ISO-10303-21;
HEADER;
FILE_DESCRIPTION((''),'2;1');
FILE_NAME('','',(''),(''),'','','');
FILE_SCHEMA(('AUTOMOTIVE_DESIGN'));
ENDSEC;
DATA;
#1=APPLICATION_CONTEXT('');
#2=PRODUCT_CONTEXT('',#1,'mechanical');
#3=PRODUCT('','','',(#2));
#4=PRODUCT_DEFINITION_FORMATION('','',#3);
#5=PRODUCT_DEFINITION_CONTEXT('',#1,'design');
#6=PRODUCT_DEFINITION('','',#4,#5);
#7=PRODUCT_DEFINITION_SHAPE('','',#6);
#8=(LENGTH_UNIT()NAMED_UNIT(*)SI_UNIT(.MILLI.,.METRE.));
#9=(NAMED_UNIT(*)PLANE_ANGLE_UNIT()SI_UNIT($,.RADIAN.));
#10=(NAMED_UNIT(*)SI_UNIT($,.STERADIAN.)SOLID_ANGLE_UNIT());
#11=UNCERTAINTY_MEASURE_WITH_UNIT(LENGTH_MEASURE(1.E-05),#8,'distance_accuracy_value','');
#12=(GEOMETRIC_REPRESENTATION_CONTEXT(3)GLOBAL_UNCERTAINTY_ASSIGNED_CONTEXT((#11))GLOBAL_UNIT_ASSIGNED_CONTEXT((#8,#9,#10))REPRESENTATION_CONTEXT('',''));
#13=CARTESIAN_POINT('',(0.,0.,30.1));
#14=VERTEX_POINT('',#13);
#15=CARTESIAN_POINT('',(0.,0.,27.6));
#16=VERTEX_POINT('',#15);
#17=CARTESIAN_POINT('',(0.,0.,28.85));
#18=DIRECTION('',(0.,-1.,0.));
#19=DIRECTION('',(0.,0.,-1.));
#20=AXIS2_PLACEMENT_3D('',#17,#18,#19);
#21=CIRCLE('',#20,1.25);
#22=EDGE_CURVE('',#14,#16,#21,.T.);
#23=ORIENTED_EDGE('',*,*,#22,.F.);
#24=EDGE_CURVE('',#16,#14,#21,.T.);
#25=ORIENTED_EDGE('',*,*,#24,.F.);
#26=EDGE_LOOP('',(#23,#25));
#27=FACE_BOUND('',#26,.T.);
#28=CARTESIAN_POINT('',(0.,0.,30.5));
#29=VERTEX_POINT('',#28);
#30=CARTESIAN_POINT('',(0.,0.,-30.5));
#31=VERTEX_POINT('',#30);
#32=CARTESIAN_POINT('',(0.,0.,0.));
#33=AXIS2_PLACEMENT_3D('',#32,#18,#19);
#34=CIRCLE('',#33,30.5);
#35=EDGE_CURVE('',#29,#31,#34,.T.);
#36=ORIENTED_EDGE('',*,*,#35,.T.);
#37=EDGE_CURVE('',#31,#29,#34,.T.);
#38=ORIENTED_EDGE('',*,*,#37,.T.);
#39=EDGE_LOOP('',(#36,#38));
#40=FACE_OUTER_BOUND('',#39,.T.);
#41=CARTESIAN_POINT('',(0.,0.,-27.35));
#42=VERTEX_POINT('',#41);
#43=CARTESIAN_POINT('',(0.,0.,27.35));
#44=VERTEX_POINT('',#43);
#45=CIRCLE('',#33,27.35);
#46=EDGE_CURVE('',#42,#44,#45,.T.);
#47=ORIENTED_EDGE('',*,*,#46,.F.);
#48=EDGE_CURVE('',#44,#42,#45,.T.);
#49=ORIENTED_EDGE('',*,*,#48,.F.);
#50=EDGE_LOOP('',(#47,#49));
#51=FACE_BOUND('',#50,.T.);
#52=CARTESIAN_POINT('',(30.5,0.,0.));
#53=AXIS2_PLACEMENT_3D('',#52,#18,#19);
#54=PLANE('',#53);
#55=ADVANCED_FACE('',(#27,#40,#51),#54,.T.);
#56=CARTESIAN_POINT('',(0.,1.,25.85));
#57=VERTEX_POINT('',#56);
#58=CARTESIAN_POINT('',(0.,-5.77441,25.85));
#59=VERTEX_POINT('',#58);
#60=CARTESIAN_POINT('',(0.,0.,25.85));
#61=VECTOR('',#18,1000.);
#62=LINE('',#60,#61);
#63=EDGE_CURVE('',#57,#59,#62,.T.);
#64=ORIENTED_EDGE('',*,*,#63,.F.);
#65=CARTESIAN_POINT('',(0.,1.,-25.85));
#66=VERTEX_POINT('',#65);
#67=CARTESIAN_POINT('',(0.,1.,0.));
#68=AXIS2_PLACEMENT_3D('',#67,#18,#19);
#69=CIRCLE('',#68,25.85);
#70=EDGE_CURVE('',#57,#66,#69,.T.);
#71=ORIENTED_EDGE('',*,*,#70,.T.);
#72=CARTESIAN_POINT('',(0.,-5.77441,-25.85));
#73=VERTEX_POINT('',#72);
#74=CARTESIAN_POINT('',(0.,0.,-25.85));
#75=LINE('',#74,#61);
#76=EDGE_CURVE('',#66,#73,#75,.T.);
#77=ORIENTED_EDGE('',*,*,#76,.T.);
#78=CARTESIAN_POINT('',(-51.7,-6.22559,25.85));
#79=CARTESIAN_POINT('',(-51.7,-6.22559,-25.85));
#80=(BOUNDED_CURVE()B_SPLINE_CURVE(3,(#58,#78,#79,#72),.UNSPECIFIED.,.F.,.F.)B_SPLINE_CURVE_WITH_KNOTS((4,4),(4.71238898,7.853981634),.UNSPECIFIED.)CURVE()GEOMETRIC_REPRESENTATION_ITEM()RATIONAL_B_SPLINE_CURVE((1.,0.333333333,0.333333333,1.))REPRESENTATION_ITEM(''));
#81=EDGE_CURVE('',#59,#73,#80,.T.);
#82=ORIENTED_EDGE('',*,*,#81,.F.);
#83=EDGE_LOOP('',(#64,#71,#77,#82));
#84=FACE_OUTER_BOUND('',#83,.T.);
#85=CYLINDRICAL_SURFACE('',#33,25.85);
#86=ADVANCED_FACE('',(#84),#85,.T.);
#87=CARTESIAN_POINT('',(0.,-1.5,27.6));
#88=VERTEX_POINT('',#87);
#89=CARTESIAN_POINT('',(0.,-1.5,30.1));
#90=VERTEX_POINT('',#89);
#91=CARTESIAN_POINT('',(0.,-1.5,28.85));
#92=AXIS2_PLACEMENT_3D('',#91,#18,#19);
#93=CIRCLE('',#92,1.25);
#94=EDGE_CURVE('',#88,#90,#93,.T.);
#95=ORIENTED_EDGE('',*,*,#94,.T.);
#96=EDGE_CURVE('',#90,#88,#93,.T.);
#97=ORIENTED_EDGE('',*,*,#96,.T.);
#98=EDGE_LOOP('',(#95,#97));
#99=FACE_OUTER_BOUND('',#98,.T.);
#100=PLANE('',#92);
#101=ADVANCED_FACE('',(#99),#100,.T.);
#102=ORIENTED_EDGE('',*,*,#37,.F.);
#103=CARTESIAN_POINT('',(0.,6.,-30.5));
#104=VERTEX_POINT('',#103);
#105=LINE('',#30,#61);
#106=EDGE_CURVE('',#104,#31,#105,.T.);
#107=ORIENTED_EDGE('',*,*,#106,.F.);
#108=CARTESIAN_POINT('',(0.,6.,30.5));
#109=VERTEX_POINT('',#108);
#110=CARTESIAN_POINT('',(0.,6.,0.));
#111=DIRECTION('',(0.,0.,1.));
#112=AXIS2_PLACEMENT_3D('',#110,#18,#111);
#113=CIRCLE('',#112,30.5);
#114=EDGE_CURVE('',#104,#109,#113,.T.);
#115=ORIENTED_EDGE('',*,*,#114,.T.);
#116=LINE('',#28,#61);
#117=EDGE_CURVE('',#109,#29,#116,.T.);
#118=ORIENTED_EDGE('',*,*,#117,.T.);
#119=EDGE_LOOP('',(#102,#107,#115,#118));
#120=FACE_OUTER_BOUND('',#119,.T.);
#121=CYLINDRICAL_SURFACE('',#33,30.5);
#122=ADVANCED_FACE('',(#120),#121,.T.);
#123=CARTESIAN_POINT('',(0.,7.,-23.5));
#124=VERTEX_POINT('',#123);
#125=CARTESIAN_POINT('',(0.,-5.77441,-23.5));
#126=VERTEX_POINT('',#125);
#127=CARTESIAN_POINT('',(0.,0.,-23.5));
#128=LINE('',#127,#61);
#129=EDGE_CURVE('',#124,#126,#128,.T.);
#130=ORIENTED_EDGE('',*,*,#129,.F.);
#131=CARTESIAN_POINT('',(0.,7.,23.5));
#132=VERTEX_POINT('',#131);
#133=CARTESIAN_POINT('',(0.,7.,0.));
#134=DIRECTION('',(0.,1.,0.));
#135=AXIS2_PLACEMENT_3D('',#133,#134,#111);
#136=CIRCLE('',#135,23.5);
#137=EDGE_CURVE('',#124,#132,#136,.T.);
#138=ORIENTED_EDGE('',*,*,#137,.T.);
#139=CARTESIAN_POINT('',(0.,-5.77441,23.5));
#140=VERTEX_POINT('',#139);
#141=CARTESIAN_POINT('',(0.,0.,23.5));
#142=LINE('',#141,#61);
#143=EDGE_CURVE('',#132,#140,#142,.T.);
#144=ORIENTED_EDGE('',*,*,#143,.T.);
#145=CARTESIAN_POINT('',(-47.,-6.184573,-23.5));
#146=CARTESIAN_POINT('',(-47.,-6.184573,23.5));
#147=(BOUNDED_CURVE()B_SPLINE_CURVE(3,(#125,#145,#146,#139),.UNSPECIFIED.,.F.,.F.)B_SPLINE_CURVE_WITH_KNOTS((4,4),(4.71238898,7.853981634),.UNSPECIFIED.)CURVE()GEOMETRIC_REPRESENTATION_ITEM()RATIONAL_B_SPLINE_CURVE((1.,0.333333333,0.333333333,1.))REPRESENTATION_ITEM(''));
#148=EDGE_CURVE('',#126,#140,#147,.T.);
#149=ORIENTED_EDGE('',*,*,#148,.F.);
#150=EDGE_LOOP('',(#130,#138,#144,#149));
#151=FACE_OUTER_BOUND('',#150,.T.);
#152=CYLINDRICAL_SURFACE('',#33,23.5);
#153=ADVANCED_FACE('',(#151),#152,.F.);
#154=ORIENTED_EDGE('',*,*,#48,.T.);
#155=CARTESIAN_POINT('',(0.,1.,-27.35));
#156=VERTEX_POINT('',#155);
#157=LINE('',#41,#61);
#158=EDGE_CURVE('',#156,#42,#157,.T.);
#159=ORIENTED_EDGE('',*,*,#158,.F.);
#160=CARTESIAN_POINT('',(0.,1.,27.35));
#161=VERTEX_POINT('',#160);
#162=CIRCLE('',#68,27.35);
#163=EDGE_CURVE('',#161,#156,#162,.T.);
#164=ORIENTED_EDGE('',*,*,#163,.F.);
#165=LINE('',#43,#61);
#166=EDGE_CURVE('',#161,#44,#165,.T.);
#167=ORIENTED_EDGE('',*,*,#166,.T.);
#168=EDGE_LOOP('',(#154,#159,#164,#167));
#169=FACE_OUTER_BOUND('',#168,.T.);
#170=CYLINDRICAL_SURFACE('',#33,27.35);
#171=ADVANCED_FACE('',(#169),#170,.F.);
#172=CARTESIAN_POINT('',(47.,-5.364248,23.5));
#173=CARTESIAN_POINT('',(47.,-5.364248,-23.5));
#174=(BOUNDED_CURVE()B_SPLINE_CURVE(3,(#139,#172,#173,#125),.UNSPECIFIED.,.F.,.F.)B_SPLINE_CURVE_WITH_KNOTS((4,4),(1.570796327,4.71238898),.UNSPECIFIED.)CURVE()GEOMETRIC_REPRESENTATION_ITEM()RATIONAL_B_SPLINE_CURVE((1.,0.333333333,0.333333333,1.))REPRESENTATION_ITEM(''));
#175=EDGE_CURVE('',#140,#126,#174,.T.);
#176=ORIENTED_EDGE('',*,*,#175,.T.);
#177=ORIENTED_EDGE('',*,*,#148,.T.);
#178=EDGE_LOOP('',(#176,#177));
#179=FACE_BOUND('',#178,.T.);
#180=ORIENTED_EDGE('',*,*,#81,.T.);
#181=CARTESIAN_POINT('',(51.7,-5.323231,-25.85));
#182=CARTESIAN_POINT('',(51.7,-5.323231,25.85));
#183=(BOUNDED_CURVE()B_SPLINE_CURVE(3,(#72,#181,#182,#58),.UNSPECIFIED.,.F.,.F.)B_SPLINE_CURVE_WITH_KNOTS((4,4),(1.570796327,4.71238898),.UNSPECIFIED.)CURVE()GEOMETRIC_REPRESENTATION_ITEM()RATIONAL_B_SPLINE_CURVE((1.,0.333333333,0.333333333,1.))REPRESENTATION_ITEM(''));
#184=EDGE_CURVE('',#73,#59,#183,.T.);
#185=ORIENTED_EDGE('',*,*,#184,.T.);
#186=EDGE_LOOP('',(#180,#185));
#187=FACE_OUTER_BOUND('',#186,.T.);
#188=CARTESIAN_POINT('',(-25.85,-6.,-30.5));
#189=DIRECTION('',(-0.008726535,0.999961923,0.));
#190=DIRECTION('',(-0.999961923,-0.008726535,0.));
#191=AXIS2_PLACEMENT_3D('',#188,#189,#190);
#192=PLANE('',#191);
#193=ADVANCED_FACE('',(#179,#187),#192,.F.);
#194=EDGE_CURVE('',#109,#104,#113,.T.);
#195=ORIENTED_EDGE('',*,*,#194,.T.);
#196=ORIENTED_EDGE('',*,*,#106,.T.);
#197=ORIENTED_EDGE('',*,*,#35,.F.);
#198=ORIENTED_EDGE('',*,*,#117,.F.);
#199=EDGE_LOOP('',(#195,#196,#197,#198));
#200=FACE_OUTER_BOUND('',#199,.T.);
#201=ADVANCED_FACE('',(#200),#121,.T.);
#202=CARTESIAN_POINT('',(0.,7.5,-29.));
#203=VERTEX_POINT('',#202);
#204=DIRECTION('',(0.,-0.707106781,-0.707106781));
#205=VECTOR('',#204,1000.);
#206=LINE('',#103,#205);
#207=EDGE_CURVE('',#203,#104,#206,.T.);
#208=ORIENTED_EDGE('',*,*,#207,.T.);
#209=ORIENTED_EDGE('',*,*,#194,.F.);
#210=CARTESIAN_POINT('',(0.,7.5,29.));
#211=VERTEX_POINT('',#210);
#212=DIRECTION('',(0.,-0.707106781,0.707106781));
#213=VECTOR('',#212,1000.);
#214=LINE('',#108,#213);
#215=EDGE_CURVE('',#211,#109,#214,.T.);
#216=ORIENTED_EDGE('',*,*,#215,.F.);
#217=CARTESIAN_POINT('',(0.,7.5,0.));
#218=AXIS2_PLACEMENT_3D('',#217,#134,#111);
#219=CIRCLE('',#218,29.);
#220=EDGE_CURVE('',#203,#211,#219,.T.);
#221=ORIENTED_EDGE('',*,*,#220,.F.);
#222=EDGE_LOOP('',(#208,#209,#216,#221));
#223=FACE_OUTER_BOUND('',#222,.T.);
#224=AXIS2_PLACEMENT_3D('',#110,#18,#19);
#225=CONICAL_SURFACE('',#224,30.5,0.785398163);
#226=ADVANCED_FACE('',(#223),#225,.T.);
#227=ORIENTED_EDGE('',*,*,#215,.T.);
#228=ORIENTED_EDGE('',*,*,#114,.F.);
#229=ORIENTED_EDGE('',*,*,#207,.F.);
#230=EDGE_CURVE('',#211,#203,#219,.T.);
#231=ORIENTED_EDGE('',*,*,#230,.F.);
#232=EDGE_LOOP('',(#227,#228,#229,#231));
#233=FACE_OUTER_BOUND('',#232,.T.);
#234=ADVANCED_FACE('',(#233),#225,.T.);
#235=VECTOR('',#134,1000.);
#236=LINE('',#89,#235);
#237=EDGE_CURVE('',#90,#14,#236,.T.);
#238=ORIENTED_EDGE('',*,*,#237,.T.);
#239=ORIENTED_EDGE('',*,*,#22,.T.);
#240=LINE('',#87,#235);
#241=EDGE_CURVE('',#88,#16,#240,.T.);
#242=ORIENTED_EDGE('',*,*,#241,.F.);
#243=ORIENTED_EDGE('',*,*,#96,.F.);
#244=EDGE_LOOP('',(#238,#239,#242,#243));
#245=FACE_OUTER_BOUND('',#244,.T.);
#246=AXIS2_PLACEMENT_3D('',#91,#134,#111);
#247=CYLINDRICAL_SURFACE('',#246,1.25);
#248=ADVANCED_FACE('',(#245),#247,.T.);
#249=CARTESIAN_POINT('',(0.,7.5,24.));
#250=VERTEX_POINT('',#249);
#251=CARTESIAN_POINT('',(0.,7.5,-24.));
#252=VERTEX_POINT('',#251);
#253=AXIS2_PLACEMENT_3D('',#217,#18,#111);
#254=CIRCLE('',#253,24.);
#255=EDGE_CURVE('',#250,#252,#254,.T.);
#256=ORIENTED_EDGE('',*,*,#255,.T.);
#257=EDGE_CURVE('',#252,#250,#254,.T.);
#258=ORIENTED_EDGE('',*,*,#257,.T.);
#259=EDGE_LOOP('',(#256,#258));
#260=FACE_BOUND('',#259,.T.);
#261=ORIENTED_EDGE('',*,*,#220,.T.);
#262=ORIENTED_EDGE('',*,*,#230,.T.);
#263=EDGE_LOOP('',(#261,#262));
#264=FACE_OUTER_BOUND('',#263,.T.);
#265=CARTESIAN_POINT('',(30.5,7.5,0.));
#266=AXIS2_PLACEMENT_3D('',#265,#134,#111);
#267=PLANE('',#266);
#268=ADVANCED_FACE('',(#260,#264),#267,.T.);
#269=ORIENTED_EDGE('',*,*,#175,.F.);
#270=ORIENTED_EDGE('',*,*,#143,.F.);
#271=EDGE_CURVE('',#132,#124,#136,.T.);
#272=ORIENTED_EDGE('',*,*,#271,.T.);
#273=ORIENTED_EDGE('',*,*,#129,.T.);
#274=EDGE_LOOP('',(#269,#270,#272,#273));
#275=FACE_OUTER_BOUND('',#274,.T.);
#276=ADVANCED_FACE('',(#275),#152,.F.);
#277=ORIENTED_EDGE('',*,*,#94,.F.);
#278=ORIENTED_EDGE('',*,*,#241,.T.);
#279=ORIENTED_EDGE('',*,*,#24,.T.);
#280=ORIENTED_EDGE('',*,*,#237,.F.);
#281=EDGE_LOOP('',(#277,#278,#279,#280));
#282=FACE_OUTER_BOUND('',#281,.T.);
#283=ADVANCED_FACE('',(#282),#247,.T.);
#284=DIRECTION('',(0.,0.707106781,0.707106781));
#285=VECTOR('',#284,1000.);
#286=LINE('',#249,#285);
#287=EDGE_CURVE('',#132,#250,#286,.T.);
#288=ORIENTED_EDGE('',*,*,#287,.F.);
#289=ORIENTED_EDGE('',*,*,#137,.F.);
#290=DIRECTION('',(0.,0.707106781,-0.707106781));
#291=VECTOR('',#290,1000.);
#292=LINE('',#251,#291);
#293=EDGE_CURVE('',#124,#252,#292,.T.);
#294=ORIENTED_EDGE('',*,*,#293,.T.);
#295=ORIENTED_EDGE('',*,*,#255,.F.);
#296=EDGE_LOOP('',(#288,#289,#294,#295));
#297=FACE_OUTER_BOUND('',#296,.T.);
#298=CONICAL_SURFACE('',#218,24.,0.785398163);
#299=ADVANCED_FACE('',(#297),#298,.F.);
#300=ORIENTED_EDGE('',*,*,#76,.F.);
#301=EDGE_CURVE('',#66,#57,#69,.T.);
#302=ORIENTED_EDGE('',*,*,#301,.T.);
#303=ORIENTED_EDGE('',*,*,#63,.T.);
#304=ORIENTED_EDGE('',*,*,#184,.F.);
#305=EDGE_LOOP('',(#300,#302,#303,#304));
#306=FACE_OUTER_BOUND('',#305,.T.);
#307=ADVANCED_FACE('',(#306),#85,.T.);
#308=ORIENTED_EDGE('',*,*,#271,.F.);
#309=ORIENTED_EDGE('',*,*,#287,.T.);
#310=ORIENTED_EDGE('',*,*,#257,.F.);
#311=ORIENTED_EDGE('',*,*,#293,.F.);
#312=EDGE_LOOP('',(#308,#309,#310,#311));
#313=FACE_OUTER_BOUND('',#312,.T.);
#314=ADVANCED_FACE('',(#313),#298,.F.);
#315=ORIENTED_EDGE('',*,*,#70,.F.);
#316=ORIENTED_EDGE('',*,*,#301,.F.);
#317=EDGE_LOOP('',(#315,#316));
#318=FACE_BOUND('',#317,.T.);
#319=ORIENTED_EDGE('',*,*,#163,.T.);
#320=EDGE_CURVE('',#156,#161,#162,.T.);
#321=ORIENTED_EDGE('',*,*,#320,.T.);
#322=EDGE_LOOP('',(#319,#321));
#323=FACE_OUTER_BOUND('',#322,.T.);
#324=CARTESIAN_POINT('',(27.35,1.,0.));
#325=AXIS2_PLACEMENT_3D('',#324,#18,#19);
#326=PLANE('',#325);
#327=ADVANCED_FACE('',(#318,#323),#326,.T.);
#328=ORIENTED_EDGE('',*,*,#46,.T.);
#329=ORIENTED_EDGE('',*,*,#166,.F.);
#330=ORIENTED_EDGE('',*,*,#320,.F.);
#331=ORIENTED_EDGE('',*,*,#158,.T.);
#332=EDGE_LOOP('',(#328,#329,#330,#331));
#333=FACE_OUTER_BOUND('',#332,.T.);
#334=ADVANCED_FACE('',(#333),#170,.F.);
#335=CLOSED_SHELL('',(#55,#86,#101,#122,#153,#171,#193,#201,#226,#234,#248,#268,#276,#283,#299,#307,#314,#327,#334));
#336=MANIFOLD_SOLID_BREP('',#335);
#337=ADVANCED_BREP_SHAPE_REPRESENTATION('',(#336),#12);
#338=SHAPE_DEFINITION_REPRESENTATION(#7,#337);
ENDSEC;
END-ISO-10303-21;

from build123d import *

# Parameters (mm, degrees)
CUT_EXTRUDE_1_DEPTH      = 44.780703512
CUT_EXTRUDE_1_DEPTH_BACK = 44.780703512
CHAMFER_1_SIZE           = 0.5
CHAMFER_2_SIZE           = 1.5
SKETCH_3_R               = 1.25
EXTRUDE_1_DEPTH          = 1.5


with BuildPart() as part:
    # 草图1 → 旋转1 (revolve)
    with BuildSketch(Plane.XY, mode=Mode.PRIVATE) as revolve_1_sk:
        Polygon((23.5, -7.5), (23.5, 7.5), (30.5, 7.5), (30.5, 0), (27.35, 0), (27.35, 1), (25.85, 1), (25.85, -7.5), align=None)
    revolve(revolve_1_sk.sketch.rotate(Axis((0, 0, 0), (0, 1, 0)), 90), axis=Axis((0, 0, 0), (0, 1, 0)))

    # 草图2 → 切除-拉伸1 (cut, two sides: drawn at the far end of the back side and taken through both)
    with BuildSketch(Plane.XY.offset(-CUT_EXTRUDE_1_DEPTH_BACK)):
        Polygon((-25.85, -6), (25.85, -5.548820935), (25.85, -7.5), (-25.85, -7.5), align=None)
    extrude(amount=CUT_EXTRUDE_1_DEPTH + CUT_EXTRUDE_1_DEPTH_BACK, mode=Mode.SUBTRACT)

    # 倒角1
    chamfer_1_edges = [part.edges().sort_by_distance(p)[0] for p in [
        (0, 7.5, 23.5),
    ]]
    chamfer(chamfer_1_edges, length=CHAMFER_1_SIZE)

    # 倒角2
    chamfer_2_edges = [part.edges().sort_by_distance(p)[0] for p in [
        (0, 7.5, 30.5),
    ]]
    chamfer(chamfer_2_edges, length=CHAMFER_2_SIZE)

    # 草图3 → 凸台-拉伸1 (add)
    with BuildSketch(Plane.XZ):
        with Locations(Location((0, 28.85, 0), (0, 0, 270))):
            Circle(SKETCH_3_R)
    extrude(amount=EXTRUDE_1_DEPTH)


solid = part.part
